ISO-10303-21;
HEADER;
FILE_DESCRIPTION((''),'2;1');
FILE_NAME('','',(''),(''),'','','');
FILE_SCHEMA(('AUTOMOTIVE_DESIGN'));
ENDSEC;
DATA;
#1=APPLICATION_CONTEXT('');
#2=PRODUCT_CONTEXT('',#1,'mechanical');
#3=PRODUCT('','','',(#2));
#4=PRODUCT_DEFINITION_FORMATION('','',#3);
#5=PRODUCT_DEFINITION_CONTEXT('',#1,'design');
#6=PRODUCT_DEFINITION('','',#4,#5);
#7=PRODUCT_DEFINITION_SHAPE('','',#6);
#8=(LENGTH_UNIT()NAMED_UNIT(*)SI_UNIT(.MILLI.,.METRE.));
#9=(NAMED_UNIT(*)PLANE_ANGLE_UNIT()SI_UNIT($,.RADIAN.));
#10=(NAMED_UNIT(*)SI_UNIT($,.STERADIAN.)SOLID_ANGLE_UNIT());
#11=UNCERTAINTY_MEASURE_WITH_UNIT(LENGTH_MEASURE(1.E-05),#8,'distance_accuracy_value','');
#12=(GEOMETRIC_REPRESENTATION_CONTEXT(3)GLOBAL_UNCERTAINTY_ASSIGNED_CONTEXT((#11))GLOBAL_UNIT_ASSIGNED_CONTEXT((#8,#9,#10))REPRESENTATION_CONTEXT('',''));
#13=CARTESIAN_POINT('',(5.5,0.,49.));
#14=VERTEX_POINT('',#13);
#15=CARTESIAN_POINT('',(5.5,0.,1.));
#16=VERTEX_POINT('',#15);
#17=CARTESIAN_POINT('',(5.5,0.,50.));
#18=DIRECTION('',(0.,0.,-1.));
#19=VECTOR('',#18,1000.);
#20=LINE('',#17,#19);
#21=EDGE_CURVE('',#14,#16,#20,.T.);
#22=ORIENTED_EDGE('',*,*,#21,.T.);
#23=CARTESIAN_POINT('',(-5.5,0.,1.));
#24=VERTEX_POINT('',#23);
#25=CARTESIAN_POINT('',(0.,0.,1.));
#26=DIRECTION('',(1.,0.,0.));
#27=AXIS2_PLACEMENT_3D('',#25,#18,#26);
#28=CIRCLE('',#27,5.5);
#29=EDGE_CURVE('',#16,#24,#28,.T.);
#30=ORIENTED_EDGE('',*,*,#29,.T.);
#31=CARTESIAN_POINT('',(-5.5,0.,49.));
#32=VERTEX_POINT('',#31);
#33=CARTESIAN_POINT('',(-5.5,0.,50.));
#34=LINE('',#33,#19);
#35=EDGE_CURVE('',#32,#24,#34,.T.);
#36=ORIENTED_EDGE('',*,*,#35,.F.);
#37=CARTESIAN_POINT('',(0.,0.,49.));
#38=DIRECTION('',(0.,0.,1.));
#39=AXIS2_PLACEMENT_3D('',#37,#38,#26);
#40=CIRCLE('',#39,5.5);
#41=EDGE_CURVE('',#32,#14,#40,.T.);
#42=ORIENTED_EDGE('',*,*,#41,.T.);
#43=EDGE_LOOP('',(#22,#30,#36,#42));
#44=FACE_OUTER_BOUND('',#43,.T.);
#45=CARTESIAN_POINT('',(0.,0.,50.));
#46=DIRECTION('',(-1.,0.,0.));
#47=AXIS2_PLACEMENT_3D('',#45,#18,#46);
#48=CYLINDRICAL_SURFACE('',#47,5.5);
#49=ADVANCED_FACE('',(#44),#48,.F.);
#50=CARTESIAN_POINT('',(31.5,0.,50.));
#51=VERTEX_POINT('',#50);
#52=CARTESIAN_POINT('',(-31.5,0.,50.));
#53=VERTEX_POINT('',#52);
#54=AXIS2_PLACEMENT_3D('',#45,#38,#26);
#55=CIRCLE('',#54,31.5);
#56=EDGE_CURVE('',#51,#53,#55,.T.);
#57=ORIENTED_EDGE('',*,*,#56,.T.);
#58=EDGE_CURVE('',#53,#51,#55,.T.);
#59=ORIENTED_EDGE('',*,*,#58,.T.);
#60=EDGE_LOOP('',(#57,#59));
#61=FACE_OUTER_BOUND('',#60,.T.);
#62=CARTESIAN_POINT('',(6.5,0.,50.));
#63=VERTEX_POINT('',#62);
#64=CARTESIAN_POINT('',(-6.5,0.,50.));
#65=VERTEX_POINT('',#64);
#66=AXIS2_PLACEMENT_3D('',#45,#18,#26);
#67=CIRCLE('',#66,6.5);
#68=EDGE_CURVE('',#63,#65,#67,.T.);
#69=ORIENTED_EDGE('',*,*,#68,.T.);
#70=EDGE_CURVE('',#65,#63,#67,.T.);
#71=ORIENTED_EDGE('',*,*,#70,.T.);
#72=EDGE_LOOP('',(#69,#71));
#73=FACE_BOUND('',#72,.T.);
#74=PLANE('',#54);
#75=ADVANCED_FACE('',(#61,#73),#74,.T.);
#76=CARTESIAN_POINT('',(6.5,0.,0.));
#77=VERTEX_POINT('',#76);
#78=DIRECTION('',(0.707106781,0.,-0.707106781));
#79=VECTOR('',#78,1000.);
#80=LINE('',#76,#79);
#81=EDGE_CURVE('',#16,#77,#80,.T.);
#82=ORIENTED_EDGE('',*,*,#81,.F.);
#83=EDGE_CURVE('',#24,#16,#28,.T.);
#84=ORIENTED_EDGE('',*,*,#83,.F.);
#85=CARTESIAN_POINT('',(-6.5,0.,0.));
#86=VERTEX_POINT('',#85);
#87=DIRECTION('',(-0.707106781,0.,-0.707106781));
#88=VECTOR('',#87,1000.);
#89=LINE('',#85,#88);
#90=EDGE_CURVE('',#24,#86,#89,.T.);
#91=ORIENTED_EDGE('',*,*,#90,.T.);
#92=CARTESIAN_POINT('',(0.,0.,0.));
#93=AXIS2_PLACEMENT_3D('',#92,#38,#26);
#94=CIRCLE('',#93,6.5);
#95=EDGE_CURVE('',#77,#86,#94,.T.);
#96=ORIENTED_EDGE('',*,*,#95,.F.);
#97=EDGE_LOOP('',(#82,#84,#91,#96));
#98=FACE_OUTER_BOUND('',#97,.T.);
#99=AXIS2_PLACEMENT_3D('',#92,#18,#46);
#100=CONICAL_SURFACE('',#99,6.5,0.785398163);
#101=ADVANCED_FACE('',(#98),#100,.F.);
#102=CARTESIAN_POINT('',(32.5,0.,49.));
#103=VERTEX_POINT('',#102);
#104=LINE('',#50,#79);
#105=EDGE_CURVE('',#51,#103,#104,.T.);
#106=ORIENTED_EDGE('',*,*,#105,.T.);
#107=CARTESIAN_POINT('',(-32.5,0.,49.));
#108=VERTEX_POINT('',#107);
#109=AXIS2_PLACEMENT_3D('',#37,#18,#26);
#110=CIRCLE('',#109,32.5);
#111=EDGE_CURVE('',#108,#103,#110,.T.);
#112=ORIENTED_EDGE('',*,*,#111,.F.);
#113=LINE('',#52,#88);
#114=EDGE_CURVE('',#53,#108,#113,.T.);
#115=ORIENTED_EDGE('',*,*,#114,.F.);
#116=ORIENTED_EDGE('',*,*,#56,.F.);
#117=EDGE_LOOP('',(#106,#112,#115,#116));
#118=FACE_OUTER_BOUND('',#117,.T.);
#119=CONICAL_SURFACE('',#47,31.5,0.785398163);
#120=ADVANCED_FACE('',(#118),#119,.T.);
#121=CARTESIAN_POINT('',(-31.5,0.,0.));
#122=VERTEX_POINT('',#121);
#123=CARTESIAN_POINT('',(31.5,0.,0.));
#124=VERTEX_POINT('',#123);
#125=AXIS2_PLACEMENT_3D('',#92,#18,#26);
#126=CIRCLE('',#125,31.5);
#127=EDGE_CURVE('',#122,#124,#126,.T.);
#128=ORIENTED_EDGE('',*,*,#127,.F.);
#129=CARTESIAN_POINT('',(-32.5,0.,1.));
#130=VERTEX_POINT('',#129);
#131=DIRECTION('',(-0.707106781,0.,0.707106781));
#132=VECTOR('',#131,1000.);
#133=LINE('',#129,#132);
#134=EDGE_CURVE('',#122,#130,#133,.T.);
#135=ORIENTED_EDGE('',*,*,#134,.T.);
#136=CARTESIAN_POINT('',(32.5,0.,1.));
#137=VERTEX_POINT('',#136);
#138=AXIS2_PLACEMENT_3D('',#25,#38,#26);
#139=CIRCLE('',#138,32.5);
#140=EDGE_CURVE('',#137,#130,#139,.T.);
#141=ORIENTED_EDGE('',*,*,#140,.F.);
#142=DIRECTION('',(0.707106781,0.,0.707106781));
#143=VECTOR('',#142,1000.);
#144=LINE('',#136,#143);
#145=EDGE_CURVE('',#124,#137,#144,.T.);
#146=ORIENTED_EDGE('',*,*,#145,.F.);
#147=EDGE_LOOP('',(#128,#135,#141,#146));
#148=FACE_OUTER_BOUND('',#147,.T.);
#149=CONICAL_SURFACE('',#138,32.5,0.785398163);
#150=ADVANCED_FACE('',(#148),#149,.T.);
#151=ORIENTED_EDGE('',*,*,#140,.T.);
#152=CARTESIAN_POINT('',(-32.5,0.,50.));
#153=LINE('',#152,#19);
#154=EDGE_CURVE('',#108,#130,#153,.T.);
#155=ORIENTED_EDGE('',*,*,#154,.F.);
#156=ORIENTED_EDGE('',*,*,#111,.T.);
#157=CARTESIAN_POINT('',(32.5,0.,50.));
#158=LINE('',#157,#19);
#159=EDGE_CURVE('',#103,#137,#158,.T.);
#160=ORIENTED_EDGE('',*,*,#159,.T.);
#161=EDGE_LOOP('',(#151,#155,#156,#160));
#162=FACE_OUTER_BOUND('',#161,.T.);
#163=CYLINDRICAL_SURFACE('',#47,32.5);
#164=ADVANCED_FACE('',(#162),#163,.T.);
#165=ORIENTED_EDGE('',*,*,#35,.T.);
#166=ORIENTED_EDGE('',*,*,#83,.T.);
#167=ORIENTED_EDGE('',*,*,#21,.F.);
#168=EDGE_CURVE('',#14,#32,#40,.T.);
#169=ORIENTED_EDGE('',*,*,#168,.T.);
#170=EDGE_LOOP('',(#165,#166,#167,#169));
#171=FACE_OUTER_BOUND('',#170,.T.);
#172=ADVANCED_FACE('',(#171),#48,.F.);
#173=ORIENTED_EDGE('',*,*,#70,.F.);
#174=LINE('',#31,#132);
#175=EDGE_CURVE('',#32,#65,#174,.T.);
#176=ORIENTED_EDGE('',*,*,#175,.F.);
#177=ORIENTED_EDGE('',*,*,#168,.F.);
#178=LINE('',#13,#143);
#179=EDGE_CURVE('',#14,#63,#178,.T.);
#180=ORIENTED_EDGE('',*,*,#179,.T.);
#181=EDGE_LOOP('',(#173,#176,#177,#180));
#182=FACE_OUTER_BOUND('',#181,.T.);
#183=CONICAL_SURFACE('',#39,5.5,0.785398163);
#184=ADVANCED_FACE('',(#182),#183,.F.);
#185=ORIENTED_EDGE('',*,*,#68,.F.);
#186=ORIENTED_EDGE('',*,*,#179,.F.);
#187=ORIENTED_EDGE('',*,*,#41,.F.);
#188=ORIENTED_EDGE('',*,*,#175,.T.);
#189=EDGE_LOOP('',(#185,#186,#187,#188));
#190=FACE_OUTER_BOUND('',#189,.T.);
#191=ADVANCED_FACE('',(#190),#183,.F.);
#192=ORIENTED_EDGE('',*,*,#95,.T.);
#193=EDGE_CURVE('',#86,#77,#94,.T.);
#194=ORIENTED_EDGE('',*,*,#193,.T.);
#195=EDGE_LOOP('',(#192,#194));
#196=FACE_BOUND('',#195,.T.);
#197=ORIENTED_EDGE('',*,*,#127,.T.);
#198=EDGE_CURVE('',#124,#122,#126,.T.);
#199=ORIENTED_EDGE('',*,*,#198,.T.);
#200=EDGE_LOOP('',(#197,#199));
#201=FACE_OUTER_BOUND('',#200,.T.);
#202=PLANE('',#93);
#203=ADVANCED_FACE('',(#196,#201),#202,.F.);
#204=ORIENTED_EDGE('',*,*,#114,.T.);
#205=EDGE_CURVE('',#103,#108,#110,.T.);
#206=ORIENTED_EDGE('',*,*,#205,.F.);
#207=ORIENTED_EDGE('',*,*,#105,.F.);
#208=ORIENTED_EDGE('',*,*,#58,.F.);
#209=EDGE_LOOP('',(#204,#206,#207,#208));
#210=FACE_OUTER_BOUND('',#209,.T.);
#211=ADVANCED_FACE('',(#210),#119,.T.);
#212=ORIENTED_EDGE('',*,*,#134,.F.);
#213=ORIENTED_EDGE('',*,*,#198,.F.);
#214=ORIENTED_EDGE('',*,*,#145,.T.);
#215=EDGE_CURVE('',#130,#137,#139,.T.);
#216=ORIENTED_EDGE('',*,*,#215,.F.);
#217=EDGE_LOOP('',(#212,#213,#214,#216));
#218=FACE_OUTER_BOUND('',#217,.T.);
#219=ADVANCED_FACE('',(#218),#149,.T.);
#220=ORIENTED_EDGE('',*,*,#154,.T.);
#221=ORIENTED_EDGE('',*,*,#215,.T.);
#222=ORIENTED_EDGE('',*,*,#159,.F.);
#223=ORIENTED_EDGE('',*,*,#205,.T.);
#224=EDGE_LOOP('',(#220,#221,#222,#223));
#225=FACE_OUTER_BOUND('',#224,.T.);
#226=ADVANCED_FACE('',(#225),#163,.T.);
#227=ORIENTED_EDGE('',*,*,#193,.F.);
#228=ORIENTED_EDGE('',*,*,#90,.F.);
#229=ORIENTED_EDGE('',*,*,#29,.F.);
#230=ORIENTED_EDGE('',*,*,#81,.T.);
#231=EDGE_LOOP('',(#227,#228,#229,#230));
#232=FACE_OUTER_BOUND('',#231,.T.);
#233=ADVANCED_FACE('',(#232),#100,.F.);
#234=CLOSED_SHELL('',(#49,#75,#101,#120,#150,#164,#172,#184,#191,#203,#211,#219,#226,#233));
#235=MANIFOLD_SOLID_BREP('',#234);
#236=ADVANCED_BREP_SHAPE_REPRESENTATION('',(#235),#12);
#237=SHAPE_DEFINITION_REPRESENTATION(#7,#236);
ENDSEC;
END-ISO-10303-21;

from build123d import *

# Parameters (mm, degrees)
SKETCH_1_R      = 32.5
SKETCH_1_R_2    = 5.5
EXTRUDE_1_DEPTH = 50
CHAMFER_1_SIZE  = 1


with BuildPart() as part:
    # 草图1 → 凸台-拉伸1 (new body)
    with BuildSketch(Plane.XY):
        Circle(SKETCH_1_R)
        Circle(SKETCH_1_R_2, mode=Mode.SUBTRACT)
    extrude(amount=EXTRUDE_1_DEPTH)

    # 倒角1
    chamfer_1_edges = [part.edges().sort_by_distance(p)[0] for p in [
        (-32.5, 0, 0),
        (-32.5, 0, 50),
        (-5.5, 0, 0),
        (-5.5, 0, 50),
    ]]
    chamfer(chamfer_1_edges, length=CHAMFER_1_SIZE)


solid = part.part
